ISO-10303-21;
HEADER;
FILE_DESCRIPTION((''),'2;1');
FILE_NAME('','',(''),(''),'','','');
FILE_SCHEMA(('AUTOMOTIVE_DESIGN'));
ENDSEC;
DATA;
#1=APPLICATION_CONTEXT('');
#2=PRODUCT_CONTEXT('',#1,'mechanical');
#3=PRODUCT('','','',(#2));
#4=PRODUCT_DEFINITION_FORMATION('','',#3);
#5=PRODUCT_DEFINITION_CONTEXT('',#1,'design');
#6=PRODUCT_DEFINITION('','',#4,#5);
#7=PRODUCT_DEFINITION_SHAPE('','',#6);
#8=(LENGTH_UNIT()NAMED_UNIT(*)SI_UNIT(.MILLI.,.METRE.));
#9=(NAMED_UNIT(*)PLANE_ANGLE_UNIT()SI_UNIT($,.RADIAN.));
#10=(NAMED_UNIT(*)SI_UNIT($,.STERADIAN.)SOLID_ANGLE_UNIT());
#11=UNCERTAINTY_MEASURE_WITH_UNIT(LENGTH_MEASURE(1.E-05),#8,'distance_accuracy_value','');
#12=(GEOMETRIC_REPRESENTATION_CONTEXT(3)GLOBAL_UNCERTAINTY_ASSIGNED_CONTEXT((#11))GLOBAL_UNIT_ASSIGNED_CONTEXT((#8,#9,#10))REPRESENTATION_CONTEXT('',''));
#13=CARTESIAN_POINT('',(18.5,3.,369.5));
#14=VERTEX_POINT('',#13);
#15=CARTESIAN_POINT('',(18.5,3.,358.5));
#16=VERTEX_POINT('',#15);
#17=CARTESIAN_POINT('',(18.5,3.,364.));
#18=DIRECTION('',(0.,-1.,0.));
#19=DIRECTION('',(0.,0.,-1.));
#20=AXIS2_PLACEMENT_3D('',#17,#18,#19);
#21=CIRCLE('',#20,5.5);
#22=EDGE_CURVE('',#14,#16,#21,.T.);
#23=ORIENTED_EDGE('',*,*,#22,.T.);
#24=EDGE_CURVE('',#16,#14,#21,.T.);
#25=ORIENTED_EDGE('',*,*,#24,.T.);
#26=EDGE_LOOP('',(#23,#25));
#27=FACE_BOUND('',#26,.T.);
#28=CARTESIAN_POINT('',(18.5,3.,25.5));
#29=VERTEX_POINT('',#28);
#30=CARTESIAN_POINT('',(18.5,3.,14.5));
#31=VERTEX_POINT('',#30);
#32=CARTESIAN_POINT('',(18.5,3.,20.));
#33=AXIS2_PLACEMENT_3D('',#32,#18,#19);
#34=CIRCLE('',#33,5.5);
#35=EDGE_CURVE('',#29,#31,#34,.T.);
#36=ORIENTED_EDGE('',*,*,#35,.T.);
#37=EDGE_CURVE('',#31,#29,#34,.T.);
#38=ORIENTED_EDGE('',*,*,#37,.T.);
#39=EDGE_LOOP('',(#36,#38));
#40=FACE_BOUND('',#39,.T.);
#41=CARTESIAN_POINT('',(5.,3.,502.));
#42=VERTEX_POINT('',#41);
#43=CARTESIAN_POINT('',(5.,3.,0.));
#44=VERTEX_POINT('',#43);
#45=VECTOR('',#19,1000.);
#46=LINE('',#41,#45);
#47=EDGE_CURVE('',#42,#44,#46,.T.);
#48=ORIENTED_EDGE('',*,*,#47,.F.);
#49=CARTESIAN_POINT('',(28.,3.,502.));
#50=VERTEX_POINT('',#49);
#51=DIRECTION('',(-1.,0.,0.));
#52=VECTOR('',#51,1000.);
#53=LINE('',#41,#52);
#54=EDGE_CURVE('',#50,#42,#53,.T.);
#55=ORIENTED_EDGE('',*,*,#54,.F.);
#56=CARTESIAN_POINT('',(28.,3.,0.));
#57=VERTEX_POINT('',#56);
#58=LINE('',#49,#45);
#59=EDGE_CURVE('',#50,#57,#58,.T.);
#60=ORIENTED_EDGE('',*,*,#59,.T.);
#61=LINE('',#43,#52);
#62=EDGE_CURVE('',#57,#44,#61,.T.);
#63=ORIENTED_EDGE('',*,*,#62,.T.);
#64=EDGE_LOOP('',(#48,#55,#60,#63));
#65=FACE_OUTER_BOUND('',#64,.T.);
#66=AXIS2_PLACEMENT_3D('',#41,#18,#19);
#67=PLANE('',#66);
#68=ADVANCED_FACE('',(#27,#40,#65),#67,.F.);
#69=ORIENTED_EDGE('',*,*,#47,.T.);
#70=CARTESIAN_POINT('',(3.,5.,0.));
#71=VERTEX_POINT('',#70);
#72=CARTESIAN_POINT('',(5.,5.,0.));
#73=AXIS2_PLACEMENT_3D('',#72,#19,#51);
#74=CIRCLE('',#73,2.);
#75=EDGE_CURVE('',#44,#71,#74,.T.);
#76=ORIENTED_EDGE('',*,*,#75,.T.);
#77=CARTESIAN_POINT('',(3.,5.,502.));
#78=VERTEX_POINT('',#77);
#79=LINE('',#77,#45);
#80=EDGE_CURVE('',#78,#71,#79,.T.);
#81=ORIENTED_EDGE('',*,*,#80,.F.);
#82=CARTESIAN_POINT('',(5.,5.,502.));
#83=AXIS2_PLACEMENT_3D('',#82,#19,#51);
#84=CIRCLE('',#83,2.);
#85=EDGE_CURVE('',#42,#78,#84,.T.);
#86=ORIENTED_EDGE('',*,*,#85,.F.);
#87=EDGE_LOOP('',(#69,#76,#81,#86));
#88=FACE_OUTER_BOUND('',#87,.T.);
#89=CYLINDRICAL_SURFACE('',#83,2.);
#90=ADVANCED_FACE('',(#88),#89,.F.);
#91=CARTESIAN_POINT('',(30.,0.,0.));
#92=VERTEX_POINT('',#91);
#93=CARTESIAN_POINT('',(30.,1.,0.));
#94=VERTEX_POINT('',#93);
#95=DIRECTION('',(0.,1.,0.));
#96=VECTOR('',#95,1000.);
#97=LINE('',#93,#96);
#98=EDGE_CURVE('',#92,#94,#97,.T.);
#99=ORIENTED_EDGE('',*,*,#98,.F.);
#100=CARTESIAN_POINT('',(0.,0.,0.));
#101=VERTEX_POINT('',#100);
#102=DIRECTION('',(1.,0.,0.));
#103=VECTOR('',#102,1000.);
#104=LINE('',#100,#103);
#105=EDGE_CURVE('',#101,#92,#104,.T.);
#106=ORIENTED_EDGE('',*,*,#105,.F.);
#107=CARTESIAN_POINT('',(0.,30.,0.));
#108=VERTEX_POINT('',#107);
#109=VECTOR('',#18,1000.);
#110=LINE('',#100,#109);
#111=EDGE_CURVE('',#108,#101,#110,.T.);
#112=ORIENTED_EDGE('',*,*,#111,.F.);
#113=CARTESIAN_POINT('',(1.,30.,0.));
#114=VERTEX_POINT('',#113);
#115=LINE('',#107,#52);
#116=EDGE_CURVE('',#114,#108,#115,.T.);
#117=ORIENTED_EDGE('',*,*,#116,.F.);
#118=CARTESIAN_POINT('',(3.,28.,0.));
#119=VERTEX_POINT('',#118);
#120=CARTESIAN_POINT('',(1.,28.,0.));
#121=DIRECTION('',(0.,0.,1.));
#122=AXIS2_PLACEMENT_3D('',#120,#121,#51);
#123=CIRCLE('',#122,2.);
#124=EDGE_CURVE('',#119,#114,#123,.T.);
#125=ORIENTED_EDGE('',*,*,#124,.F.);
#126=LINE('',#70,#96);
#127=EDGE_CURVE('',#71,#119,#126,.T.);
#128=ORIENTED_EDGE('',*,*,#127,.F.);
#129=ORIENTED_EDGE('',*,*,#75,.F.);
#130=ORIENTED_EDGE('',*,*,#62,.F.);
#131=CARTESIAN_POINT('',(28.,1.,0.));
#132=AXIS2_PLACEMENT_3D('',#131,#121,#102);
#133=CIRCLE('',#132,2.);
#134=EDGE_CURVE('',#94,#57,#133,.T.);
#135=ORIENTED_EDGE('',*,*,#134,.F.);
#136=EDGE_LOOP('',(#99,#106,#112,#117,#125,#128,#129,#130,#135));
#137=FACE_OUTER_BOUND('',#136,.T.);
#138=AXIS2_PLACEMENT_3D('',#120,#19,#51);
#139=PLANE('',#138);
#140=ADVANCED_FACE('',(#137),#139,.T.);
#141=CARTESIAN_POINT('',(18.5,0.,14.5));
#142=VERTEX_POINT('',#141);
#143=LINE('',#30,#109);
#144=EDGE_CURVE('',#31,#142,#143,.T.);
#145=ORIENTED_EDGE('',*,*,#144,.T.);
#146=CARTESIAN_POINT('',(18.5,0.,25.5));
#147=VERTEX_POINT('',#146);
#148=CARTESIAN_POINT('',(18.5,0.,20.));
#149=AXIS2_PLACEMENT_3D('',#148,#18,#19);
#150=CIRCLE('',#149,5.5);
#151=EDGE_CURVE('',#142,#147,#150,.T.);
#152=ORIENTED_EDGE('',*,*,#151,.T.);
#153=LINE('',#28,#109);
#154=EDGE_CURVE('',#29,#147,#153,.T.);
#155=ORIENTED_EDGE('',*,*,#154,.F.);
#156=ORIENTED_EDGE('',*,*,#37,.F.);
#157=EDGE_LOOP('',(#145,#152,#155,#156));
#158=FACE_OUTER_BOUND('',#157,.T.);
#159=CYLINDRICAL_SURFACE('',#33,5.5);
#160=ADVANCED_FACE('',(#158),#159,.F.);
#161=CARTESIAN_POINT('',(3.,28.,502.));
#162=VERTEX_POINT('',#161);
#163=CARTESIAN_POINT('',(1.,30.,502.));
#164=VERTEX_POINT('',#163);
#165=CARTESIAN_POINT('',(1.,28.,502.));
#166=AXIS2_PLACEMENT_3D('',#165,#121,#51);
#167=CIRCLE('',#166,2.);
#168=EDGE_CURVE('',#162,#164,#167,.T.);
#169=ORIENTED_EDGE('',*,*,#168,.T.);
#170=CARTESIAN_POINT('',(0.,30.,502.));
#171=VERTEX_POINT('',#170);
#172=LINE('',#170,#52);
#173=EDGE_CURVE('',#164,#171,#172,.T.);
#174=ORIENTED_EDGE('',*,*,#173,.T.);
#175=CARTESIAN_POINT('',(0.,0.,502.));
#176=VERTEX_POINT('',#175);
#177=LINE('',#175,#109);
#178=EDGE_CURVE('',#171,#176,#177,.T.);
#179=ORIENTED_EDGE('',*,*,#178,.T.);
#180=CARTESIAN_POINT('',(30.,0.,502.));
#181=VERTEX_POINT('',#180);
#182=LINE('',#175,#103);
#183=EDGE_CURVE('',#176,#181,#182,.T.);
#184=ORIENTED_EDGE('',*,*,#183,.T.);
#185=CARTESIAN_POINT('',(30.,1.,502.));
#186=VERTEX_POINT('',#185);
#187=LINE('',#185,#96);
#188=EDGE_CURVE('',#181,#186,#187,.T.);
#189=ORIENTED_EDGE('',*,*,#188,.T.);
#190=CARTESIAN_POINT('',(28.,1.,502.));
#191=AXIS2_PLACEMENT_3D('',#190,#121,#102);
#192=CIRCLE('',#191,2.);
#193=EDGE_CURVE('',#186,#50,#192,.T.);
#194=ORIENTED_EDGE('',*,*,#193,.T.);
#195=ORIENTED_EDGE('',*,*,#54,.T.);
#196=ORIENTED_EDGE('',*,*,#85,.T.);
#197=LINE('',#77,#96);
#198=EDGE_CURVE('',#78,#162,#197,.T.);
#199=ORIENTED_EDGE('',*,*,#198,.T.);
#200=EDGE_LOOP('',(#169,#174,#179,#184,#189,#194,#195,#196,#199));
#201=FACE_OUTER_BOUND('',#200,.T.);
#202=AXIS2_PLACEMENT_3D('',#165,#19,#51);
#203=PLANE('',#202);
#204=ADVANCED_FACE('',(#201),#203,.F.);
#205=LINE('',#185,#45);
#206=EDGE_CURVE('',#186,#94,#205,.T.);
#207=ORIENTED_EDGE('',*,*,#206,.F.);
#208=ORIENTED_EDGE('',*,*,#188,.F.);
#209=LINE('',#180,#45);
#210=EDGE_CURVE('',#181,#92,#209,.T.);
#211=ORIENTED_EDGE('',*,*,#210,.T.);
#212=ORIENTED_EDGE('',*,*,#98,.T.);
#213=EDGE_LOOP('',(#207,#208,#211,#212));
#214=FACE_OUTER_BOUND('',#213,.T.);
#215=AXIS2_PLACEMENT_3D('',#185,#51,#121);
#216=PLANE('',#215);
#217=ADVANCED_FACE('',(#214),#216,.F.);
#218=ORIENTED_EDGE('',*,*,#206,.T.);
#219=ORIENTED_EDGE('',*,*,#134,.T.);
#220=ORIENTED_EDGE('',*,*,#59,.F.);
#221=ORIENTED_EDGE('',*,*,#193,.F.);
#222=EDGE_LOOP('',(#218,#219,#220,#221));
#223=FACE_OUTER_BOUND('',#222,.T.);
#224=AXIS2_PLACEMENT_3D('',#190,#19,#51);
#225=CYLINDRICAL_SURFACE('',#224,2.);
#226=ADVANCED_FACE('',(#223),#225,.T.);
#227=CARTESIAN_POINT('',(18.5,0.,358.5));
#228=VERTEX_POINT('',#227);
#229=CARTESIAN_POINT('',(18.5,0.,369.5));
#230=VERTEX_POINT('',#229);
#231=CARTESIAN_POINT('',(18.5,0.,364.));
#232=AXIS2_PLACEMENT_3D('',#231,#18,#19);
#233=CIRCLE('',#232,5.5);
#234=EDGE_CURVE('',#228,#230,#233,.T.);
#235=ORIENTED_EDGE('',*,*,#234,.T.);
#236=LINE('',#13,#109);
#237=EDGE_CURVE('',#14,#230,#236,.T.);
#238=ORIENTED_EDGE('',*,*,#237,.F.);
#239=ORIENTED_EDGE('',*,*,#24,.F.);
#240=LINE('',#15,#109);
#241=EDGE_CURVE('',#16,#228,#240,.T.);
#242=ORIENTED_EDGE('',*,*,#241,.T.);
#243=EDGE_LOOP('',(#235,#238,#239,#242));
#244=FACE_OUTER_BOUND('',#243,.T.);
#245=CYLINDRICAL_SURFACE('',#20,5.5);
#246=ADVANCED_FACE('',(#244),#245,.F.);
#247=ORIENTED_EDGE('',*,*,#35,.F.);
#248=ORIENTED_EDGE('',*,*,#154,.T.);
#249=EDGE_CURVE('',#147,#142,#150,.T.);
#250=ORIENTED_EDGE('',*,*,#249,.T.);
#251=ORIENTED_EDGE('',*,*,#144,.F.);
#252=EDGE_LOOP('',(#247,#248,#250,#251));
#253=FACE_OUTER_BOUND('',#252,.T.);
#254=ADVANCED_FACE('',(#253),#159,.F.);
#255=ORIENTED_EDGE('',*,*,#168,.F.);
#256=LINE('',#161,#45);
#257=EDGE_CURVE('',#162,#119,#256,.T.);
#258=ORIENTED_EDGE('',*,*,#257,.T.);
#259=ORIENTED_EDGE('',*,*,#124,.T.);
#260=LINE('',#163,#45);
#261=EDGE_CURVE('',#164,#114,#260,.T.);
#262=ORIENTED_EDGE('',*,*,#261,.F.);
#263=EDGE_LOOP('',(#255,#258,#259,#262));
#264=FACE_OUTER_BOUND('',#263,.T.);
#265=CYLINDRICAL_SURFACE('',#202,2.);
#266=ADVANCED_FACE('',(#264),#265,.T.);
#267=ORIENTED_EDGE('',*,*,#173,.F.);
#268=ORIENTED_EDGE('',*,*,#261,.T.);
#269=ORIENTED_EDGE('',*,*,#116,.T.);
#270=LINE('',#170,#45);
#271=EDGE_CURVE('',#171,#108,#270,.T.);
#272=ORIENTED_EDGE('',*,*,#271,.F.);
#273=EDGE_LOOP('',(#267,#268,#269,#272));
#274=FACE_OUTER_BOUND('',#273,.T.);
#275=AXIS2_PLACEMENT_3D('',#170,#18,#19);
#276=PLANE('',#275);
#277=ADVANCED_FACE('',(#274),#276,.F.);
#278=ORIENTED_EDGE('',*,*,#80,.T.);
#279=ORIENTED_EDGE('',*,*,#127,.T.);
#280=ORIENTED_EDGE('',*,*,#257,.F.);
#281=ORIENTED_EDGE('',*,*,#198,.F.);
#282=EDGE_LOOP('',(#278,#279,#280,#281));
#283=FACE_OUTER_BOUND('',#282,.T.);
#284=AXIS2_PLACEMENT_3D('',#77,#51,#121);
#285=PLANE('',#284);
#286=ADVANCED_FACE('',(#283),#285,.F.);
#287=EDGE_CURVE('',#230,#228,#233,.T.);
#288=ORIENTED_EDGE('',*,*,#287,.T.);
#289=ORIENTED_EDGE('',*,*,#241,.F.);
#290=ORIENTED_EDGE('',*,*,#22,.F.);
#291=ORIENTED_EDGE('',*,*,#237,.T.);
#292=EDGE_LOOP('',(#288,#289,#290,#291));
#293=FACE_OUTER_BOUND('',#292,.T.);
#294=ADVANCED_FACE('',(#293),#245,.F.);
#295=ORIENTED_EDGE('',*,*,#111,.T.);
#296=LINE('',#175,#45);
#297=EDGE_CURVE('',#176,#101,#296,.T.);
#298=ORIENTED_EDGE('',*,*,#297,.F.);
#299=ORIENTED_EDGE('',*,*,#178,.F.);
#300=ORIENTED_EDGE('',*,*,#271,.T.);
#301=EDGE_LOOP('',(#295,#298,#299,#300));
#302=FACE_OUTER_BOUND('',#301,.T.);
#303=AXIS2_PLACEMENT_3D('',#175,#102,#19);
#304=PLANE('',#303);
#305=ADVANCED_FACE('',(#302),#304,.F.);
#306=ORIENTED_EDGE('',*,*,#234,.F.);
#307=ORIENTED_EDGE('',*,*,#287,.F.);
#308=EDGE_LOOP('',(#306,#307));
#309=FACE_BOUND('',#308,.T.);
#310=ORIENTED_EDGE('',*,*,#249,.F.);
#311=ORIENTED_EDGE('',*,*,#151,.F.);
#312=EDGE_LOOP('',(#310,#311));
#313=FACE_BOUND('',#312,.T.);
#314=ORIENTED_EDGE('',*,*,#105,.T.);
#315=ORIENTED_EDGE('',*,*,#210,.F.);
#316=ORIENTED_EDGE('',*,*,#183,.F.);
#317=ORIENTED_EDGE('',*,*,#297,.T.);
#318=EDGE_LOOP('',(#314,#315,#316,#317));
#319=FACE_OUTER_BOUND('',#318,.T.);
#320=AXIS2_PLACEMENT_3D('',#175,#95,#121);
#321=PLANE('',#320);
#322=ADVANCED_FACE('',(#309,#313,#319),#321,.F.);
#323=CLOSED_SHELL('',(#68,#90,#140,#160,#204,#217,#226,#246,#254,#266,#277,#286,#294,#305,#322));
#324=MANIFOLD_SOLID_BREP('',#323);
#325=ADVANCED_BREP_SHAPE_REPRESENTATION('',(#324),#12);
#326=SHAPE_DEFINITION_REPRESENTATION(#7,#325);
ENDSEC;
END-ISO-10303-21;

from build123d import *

# Parameters (mm, degrees)
BOSS_EXTRUDE1_DEPTH = 502
SKETCH2_R           = 5.5
CUT_EXTRUDE1_DEPTH  = 3
LPATTERN1_COUNT     = 2
LPATTERN1_PITCH     = 344


with BuildPart() as part:
    # Sketch1 → Boss-Extrude1 (new body)
    with BuildSketch(Plane.XY):
        with BuildLine():
            Line((0, 0), (30, 0))
            Line((30, 0), (30, 1))
            ThreePointArc((30, 1), (29.414213562, 2.414213562), (28, 3))
            Line((28, 3), (5, 3))
            ThreePointArc((5, 3), (3.585786438, 3.585786438), (3, 5))
            Line((3, 5), (3, 28))
            ThreePointArc((3, 28), (2.414213562, 29.414213562), (1, 30))
            Line((1, 30), (0, 30))
            Line((0, 30), (0, 0))
        make_face()
    extrude(amount=BOSS_EXTRUDE1_DEPTH)

    # Sketch2 → Cut-Extrude1 (cut)
    with BuildSketch(Plane.XZ):
        with Locations(Location((18.5, 20, 0), (0, 0, 270))):
            Circle(SKETCH2_R)
    cut_extrude1 = extrude(amount=-CUT_EXTRUDE1_DEPTH, mode=Mode.SUBTRACT)

    # LPattern1: Cut-Extrude1 ×2
    with Locations(*[(0, 0, i * LPATTERN1_PITCH) for i in range(1, LPATTERN1_COUNT)]):
        add(cut_extrude1, mode=Mode.SUBTRACT)


solid = part.part
